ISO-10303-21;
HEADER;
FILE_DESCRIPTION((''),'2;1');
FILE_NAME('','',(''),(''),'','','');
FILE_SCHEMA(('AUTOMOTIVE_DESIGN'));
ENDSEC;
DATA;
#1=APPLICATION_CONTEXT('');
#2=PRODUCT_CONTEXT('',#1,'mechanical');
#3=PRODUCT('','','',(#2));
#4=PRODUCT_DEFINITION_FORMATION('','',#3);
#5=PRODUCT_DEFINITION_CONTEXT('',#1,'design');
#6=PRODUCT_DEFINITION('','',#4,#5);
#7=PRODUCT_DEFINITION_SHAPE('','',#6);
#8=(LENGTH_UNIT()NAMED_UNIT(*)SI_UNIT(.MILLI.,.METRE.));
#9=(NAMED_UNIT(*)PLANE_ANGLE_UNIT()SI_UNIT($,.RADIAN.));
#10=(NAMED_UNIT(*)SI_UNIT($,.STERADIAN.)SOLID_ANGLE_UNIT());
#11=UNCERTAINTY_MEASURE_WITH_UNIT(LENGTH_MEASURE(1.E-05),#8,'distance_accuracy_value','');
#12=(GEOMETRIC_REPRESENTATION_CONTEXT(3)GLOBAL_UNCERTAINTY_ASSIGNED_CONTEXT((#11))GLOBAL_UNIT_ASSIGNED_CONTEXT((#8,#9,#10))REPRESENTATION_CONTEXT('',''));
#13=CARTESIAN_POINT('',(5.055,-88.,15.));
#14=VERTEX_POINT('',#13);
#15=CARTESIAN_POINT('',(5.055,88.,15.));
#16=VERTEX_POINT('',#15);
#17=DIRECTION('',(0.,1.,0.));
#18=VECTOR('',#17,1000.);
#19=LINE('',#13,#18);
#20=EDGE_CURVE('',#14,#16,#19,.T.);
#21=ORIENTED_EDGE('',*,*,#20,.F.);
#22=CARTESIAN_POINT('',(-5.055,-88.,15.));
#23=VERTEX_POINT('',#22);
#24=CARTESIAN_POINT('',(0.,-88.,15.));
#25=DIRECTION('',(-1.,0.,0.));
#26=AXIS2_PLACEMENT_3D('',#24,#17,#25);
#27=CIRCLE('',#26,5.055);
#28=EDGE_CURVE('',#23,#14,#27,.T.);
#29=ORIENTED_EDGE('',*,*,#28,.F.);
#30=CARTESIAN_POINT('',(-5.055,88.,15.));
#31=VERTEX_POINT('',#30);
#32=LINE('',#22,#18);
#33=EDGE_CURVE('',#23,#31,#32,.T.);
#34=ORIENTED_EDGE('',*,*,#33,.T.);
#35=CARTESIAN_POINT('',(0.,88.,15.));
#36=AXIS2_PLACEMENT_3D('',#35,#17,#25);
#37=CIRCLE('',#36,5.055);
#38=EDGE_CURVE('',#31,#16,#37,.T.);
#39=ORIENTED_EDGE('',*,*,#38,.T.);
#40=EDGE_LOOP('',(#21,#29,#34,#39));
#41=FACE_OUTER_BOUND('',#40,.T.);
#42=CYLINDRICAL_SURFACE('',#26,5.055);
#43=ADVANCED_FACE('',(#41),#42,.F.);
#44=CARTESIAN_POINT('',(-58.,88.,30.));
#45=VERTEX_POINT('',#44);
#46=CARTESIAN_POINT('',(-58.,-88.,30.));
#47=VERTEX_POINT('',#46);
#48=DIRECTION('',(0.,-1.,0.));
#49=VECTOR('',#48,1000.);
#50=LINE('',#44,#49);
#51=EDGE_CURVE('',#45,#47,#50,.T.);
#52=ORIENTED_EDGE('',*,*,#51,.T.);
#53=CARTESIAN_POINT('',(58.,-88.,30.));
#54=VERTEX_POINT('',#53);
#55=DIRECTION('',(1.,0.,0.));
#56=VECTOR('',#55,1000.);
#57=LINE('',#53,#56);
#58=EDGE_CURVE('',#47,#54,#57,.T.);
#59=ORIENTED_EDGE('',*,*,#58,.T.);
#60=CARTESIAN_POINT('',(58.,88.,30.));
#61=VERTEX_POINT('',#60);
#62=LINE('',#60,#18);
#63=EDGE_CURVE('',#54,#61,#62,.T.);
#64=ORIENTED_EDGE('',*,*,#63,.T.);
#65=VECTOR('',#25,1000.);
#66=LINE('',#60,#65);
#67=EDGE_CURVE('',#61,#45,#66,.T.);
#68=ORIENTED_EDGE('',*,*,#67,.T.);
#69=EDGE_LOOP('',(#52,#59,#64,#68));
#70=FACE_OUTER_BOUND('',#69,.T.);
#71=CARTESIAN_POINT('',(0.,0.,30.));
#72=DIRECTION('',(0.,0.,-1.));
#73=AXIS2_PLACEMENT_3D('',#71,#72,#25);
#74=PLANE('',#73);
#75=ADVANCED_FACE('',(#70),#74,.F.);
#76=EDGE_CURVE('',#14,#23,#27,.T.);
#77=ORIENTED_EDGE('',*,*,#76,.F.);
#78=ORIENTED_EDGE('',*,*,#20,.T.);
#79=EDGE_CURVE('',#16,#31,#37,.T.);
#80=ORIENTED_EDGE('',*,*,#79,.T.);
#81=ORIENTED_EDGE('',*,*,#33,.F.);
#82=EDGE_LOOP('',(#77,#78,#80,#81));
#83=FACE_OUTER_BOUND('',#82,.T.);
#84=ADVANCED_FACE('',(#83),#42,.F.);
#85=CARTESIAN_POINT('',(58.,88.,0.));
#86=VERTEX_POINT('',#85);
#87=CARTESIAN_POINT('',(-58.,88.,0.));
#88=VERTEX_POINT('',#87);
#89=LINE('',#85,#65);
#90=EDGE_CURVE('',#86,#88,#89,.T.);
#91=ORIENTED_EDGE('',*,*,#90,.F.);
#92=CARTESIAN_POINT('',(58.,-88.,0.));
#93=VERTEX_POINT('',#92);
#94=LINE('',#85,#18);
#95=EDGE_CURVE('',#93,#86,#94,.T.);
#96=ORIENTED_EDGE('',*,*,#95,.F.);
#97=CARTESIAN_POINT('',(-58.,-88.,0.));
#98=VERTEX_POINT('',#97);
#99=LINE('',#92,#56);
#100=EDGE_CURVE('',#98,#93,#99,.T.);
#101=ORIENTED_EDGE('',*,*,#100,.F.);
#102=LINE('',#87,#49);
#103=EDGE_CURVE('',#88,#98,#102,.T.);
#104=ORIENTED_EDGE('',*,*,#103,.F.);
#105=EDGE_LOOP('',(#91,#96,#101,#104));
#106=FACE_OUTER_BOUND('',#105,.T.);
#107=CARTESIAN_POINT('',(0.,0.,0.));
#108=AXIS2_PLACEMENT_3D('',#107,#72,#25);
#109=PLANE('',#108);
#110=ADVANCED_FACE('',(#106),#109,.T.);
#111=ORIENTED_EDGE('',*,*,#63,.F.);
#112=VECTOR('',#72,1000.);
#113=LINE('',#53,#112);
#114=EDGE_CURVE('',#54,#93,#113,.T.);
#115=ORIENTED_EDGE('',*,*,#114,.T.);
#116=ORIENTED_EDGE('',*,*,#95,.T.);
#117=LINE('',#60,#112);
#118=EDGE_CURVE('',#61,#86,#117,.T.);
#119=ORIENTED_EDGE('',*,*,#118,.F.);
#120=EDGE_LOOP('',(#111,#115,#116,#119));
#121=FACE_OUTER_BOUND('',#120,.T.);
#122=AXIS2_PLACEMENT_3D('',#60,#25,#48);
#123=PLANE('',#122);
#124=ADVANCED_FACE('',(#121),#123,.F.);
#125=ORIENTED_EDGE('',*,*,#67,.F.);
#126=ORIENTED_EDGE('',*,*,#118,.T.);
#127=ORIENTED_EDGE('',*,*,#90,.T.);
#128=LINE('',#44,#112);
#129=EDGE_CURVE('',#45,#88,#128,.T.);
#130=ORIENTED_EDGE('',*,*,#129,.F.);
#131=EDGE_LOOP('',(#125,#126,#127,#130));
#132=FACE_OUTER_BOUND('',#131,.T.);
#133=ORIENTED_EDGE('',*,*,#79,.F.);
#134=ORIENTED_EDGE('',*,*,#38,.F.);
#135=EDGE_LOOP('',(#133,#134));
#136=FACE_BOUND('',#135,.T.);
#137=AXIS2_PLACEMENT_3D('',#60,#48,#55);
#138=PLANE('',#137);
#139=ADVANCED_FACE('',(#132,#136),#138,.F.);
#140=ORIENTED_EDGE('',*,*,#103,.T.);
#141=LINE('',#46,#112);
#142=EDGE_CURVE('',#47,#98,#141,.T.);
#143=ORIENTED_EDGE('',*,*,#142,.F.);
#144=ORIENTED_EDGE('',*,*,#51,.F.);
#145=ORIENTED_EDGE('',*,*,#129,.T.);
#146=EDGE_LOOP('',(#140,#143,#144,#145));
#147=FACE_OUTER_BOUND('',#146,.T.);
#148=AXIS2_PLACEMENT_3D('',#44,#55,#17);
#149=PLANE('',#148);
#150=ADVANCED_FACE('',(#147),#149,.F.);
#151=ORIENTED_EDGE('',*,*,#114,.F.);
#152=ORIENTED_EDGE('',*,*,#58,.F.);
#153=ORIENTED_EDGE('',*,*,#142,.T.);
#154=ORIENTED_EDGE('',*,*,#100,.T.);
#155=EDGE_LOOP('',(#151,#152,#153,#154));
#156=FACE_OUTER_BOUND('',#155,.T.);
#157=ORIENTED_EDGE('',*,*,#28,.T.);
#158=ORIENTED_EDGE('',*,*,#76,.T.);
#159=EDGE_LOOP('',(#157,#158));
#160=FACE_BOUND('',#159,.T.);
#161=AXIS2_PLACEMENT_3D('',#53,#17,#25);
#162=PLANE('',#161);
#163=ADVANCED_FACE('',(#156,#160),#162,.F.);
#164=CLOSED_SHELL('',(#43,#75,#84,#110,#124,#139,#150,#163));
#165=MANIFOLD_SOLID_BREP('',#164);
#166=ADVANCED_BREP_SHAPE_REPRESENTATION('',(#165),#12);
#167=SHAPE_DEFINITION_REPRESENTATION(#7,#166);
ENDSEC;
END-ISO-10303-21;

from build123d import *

# Parameters (mm, degrees)
SKETCH1_W           = 116
SKETCH1_H           = 176
BOSS_EXTRUDE1_DEPTH = 30
SKETCH3_R           = 5.055
CUT_EXTRUDE1_DEPTH  = 188.723200484


with BuildPart() as part:
    # Sketch1 → Boss-Extrude1 (new body)
    with BuildSketch(Plane.XY):
        Rectangle(SKETCH1_W, SKETCH1_H)
    extrude(amount=BOSS_EXTRUDE1_DEPTH)

    # Sketch3 → Cut-Extrude1 (cut, through all)
    with BuildSketch(Plane(origin=(0, 88, 0), x_dir=(1, 0, 0), z_dir=(0, 1, 0))):
        with Locations(Location((0, -15, 0), (0, 0, 180))):
            Circle(SKETCH3_R)
    extrude(amount=-CUT_EXTRUDE1_DEPTH, mode=Mode.SUBTRACT)


solid = part.part
